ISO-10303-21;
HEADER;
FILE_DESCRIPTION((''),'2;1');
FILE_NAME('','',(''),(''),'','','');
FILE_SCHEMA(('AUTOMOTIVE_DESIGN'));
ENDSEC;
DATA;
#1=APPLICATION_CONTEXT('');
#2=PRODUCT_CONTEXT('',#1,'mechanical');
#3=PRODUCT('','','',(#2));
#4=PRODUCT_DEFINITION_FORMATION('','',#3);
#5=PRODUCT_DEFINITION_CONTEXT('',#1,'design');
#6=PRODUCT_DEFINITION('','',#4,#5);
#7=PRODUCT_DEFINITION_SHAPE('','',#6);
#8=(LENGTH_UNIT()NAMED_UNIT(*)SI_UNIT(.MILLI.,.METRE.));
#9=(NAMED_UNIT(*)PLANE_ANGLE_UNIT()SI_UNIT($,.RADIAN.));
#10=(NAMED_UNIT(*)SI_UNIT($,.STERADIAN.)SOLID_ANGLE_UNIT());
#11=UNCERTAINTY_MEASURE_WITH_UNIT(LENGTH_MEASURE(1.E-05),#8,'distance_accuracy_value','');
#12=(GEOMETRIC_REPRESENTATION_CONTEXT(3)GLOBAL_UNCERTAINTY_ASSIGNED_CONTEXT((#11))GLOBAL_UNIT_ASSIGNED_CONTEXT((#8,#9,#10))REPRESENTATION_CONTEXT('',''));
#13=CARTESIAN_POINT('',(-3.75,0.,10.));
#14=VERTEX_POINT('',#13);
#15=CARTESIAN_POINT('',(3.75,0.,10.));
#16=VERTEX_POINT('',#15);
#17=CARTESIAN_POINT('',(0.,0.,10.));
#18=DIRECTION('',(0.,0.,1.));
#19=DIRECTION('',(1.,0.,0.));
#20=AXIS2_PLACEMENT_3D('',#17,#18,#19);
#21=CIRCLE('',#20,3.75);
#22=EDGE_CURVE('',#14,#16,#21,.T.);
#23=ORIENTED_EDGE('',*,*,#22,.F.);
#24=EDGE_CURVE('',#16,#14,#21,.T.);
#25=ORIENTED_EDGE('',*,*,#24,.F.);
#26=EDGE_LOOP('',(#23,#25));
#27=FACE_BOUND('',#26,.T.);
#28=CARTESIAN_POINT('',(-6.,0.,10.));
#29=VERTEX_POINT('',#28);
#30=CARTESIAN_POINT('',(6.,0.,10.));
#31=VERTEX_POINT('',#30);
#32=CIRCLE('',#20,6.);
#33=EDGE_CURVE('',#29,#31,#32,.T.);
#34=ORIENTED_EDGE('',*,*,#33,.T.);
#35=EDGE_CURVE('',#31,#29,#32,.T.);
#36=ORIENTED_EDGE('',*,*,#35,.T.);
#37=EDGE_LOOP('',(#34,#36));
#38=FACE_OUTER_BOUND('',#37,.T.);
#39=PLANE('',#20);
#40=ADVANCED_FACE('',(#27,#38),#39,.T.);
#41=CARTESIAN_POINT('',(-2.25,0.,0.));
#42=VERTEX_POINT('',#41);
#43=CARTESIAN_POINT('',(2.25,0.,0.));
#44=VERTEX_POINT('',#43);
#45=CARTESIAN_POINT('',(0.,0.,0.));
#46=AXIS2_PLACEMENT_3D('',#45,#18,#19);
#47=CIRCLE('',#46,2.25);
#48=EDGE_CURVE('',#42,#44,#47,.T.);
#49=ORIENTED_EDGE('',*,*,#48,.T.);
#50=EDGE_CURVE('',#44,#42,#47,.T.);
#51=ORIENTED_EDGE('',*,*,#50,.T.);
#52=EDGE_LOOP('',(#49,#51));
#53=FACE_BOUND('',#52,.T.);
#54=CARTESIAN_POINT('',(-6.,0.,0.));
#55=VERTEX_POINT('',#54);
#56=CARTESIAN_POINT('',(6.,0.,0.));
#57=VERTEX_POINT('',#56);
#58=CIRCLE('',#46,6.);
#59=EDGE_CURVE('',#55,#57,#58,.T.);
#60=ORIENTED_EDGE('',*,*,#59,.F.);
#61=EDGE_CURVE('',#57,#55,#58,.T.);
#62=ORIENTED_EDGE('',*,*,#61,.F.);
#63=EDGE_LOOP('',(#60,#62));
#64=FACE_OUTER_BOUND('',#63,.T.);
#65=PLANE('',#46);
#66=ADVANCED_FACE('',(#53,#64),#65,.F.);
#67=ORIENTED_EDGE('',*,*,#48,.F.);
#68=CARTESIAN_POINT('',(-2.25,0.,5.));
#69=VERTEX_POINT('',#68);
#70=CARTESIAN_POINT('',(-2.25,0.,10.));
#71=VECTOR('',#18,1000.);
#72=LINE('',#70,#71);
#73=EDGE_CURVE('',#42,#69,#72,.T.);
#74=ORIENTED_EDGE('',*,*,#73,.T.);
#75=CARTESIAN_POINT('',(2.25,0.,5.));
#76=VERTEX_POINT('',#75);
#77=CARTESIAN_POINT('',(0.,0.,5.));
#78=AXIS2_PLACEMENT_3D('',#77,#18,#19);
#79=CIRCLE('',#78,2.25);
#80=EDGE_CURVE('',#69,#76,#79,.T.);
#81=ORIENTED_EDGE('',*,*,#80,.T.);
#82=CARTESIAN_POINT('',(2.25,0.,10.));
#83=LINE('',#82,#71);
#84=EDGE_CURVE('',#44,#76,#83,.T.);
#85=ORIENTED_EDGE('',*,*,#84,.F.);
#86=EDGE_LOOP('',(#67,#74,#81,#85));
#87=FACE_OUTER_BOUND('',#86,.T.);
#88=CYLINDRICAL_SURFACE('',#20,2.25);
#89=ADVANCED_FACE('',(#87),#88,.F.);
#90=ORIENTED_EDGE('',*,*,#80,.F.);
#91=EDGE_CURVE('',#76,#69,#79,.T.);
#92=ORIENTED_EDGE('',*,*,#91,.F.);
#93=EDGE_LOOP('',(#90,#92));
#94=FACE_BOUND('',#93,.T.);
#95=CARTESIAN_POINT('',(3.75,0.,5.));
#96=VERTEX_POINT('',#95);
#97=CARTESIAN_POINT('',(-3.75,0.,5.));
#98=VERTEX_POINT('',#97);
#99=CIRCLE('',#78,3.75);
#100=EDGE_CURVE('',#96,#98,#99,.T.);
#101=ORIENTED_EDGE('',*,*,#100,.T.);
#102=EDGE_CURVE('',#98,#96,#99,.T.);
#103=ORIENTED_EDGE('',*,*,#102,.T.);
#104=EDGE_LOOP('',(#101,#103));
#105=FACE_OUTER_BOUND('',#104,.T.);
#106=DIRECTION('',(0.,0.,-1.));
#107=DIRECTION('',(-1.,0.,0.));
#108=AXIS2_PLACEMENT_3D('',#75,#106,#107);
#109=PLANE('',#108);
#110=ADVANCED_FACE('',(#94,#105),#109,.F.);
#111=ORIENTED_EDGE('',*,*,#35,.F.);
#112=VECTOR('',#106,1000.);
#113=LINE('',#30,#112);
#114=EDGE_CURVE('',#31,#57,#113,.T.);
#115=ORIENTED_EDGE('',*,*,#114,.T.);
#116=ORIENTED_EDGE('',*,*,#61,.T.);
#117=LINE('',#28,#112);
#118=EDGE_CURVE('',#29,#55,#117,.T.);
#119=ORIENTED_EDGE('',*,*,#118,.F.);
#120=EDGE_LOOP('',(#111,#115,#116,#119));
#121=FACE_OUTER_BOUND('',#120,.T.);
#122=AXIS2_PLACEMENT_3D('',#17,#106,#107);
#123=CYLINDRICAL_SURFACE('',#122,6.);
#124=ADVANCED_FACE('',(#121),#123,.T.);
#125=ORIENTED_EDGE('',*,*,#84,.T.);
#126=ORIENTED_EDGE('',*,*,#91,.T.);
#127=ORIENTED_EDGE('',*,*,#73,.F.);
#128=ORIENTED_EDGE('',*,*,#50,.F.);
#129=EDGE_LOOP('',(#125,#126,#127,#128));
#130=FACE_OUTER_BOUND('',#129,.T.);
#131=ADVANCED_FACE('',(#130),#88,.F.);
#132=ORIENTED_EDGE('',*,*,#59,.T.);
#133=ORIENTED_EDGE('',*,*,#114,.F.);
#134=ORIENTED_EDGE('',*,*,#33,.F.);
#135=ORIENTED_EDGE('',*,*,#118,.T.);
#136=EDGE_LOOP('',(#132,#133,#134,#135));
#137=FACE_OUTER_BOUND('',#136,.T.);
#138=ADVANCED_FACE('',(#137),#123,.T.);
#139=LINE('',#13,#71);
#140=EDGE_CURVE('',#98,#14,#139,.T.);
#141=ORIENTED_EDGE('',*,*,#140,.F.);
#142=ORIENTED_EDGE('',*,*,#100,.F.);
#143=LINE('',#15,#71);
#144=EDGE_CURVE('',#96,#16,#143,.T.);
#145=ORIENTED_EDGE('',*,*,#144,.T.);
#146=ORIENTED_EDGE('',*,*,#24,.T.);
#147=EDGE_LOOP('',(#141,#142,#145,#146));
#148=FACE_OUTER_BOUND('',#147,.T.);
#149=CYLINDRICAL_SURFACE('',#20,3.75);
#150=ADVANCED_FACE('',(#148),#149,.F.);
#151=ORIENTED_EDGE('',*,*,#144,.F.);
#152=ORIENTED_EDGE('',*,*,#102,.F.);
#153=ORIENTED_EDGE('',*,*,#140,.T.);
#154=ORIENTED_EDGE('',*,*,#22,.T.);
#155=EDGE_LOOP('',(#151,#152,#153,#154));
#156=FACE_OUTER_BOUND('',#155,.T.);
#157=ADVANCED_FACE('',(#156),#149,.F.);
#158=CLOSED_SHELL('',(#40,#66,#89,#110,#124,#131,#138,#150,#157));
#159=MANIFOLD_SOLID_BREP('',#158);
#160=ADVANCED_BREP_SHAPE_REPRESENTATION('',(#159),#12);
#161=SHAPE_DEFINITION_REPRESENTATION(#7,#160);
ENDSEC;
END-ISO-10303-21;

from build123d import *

# Parameters (mm, degrees)
SKETCH_1_R                = 6
EXTRUDE_1_DEPTH           = 10
HOLE_WIZARD_1_D           = 4.5
HOLE_WIZARD_1_CBORE_D     = 7.5
HOLE_WIZARD_1_CBORE_DEPTH = 5


with BuildPart() as part:
    # 草图1 → 凸台-拉伸1 (new body)
    with BuildSketch(Plane.XY):
        Circle(SKETCH_1_R)
    extrude(amount=EXTRUDE_1_DEPTH)

    # 打孔尺寸(%根据)内六角圆柱头螺钉的类型1 (through all)
    with Locations(Plane.XY.offset(10)):
        with Locations((0, 0)):
            CounterBoreHole(HOLE_WIZARD_1_D / 2, HOLE_WIZARD_1_CBORE_D / 2, HOLE_WIZARD_1_CBORE_DEPTH)


solid = part.part
